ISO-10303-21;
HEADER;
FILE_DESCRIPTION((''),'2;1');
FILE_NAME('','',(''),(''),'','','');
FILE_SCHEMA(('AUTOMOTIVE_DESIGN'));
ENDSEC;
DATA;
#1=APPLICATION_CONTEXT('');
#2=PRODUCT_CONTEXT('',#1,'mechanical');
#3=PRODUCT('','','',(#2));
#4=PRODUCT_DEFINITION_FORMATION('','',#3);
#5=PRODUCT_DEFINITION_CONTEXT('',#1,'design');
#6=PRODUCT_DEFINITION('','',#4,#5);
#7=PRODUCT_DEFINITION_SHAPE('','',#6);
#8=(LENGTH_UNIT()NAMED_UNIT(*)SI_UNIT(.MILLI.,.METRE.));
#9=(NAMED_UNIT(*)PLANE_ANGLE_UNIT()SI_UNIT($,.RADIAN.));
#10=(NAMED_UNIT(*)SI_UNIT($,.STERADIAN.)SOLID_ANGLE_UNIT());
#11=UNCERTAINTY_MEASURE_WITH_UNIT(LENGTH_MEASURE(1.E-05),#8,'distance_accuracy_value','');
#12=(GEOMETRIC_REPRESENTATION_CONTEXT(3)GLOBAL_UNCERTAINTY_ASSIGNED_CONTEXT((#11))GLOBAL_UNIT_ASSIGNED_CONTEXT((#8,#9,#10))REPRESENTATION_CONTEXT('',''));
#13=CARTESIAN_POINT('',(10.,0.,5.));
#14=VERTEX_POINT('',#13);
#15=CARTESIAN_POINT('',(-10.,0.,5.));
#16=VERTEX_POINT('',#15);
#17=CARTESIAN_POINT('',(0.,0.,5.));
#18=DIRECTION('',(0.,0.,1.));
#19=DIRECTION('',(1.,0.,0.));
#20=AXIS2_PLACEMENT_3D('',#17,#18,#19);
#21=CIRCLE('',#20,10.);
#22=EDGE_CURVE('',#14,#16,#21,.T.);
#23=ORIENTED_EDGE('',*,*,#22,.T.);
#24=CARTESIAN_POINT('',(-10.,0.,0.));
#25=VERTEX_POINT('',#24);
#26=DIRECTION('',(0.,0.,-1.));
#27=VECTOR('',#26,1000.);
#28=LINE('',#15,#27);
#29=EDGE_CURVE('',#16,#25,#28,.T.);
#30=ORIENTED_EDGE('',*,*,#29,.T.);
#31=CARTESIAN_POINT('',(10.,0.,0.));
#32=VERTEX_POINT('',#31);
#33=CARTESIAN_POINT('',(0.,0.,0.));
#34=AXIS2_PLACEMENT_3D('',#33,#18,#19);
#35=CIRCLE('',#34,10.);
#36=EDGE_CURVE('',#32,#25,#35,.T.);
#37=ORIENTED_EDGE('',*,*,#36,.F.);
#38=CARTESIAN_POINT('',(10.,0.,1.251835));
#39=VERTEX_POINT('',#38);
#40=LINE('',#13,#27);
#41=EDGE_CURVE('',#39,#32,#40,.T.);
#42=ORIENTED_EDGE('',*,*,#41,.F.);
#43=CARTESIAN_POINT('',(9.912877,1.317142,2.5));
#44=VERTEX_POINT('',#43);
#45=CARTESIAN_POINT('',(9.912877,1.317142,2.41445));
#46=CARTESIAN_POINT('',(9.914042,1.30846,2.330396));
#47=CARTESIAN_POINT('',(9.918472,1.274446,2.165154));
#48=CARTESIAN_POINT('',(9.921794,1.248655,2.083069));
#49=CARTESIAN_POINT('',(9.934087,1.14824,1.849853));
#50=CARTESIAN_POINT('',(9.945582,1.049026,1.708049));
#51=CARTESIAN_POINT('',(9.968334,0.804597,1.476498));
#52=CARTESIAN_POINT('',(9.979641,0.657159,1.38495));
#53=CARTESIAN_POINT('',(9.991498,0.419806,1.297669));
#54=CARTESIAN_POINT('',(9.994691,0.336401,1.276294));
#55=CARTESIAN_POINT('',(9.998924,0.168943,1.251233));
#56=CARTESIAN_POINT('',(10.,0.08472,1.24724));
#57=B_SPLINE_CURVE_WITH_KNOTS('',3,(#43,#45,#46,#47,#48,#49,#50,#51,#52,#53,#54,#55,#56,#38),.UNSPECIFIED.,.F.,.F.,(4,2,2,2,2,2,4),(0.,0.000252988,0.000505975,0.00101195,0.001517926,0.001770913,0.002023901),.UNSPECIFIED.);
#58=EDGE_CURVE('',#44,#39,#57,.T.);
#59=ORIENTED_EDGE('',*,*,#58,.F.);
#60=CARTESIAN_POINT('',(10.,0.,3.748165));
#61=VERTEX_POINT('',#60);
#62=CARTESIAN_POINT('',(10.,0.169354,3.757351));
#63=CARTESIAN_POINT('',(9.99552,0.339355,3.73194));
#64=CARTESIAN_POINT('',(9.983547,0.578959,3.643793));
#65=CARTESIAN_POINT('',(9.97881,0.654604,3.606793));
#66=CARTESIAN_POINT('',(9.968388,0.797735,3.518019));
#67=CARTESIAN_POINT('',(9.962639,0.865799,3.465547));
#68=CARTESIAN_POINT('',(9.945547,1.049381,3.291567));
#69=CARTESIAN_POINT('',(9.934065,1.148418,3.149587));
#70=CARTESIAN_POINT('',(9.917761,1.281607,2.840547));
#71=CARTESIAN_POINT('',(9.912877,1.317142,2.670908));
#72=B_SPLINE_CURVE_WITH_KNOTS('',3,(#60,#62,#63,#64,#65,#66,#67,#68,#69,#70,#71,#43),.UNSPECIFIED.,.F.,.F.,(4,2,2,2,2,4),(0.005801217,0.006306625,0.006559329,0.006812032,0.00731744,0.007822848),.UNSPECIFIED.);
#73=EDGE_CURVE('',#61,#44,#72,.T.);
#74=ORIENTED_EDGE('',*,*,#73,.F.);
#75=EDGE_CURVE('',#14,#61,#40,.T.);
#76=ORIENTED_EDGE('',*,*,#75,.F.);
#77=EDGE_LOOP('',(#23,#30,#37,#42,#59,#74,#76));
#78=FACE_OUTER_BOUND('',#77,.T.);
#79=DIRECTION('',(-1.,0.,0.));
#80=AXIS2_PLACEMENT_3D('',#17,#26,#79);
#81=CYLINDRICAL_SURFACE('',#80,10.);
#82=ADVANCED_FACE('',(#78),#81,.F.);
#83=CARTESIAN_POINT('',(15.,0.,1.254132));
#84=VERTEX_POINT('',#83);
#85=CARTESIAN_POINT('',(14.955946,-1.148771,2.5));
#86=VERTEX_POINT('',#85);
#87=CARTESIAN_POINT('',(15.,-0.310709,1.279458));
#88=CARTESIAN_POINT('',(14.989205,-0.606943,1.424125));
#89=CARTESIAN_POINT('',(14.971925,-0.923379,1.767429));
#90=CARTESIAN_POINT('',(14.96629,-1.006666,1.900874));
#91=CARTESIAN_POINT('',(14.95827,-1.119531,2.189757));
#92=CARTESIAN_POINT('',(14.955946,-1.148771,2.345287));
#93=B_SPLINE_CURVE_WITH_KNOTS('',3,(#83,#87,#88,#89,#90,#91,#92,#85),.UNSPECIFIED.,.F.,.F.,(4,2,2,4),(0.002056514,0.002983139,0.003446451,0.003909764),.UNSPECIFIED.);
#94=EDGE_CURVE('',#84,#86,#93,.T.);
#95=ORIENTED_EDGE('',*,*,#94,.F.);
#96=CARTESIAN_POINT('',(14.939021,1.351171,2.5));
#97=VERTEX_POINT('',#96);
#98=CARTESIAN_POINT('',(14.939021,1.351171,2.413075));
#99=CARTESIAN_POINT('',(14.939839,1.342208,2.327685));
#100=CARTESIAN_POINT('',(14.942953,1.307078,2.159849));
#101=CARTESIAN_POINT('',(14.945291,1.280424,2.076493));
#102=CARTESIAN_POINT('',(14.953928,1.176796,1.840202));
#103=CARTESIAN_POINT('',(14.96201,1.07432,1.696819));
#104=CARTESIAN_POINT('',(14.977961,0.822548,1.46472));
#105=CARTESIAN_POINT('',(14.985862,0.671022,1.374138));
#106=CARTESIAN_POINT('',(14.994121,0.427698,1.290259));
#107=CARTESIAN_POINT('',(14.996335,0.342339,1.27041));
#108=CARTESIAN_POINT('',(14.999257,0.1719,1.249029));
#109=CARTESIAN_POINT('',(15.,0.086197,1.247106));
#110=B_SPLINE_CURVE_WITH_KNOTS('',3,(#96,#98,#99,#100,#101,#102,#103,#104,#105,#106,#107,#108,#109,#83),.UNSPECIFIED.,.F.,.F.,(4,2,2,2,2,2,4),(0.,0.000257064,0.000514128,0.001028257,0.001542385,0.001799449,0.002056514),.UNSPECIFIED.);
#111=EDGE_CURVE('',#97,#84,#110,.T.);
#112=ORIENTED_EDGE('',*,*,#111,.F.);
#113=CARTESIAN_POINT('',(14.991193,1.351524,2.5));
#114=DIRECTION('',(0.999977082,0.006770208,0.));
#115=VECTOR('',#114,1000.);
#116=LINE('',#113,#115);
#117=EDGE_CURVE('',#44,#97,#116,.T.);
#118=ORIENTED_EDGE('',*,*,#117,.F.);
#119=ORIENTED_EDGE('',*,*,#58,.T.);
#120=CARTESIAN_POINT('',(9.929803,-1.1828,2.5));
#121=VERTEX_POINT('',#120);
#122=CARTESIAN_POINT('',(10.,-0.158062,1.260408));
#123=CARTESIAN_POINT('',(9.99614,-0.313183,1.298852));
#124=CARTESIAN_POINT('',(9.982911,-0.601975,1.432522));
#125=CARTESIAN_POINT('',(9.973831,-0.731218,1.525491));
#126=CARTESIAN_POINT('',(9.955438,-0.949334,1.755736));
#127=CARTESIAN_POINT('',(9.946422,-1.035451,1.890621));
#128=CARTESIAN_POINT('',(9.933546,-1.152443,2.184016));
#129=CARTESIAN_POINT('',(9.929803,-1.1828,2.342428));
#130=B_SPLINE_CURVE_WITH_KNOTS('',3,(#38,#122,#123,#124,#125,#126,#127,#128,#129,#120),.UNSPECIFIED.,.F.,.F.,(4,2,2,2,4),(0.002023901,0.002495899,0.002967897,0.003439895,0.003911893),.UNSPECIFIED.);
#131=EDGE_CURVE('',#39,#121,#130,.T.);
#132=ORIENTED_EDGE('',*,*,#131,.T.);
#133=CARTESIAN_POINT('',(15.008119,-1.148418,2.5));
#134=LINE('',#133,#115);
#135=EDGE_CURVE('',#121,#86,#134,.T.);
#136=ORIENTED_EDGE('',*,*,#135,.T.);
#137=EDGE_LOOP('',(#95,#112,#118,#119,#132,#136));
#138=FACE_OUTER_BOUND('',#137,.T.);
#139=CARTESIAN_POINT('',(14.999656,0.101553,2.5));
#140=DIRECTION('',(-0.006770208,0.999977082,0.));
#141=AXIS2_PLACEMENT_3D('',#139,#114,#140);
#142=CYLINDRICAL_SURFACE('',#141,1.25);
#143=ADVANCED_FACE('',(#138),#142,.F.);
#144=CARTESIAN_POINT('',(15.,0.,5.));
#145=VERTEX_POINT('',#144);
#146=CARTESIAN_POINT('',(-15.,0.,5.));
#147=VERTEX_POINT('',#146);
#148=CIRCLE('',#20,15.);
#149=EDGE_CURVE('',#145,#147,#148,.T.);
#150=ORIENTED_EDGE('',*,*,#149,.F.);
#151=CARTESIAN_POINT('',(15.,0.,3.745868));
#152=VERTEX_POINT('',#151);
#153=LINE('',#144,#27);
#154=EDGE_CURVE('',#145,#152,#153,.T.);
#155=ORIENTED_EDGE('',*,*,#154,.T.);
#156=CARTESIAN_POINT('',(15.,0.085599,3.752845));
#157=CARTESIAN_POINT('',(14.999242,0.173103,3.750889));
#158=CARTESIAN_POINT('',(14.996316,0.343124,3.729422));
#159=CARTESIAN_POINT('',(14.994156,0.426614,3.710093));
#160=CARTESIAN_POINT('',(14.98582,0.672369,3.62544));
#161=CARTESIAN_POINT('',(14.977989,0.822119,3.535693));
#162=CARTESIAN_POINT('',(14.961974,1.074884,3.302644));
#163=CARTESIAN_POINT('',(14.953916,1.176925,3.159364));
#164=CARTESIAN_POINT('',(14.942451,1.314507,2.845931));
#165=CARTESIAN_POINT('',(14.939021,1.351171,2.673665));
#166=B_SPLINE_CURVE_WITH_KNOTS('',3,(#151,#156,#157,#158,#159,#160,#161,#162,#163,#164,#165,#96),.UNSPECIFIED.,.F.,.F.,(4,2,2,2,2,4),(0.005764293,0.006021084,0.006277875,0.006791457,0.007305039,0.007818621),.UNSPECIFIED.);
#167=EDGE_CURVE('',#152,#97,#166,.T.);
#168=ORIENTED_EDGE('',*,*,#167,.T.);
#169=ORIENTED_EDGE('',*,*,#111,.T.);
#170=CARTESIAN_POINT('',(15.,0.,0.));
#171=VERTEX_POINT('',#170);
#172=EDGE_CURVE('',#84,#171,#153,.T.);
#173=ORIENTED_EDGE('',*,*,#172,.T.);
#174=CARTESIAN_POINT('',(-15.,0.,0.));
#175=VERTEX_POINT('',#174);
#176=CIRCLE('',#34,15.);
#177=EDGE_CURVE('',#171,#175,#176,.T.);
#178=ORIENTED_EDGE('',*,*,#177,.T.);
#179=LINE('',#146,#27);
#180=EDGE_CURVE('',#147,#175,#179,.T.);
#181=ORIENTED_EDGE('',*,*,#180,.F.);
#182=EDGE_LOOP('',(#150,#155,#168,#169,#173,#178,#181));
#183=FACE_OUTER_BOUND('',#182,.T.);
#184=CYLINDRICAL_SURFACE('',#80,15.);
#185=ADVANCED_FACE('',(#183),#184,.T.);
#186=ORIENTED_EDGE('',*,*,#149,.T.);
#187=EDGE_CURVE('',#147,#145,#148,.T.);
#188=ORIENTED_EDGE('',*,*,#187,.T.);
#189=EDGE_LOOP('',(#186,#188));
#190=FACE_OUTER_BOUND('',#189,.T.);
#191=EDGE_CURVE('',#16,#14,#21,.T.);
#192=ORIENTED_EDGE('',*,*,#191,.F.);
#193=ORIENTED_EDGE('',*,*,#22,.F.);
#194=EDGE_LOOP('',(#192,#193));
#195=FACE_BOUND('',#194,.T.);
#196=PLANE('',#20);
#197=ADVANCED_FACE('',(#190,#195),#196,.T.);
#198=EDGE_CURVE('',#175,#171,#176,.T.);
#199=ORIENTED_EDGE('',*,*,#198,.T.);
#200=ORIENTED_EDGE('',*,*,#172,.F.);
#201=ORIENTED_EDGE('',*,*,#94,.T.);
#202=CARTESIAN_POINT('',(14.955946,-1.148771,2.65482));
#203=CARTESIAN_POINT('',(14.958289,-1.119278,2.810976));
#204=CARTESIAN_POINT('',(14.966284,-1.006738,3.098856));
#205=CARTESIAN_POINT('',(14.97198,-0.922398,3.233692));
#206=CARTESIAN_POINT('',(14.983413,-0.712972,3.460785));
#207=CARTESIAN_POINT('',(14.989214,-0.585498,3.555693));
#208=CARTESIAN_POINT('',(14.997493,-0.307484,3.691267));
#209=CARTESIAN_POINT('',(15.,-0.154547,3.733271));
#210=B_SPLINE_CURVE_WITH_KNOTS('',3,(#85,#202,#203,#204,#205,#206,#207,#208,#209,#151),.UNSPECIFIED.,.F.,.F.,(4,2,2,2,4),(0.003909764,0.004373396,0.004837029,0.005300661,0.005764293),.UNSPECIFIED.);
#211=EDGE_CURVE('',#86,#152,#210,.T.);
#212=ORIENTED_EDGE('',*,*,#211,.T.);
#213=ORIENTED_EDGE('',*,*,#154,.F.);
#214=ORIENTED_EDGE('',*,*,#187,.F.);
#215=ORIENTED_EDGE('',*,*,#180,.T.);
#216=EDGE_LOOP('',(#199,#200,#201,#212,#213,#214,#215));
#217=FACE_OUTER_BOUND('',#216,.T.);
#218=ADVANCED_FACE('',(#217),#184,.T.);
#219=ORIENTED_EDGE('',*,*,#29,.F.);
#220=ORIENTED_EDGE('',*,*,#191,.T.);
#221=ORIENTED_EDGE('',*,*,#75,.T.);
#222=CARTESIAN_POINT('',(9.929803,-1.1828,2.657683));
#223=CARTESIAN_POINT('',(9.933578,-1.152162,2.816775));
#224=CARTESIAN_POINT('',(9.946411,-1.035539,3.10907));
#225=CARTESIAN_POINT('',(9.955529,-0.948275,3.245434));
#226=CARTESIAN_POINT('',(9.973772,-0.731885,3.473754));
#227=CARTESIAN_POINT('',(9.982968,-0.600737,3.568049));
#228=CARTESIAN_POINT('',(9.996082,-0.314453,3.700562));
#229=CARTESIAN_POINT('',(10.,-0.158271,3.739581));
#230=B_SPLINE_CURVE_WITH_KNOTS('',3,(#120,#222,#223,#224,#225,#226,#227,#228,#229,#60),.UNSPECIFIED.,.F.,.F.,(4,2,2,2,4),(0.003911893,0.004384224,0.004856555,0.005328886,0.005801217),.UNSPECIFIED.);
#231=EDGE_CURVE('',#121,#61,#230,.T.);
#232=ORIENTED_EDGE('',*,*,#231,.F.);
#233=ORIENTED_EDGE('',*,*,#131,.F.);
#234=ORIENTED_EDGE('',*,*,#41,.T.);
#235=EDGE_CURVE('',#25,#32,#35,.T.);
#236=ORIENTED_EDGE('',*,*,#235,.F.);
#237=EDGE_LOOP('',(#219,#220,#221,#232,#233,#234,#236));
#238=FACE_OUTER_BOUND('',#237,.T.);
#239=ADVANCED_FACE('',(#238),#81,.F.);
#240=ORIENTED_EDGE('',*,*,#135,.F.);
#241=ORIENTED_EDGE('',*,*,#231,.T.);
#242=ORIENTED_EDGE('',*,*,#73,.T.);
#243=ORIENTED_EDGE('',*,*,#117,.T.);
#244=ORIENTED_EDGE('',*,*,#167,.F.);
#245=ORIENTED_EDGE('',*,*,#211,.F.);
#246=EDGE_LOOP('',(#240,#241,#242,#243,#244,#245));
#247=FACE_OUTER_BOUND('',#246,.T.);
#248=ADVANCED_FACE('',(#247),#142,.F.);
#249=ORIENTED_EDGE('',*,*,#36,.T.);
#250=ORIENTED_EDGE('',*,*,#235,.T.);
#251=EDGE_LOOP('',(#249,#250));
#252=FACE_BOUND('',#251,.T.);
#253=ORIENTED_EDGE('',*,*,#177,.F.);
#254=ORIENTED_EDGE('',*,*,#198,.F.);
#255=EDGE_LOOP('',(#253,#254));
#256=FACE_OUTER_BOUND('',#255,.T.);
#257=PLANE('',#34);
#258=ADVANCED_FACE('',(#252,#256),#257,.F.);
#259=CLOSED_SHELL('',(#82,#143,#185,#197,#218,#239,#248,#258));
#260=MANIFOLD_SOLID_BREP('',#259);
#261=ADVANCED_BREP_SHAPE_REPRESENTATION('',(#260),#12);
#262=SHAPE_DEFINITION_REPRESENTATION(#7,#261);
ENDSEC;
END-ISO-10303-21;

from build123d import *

# Parameters (mm, degrees)
SKETCH_1_R             = 15
SKETCH_1_R_2           = 10
EXTRUDE_1_DEPTH        = 5
HOLE_WIZARD_M3_2_D     = 2.5
HOLE_WIZARD_M3_2_DEPTH = 7.5
HOLE_WIZARD_M3_2_TIP   = 0.751075774


with BuildPart() as part:
    # 草图1 → 凸台-拉伸1 (new body)
    with BuildSketch(Plane.XY):
        Circle(SKETCH_1_R)
        Circle(SKETCH_1_R_2, mode=Mode.SUBTRACT)
    extrude(amount=EXTRUDE_1_DEPTH)

    # M3 螺纹孔2
    with Locations(Plane(origin=(14.999656228, 0.101553124, 2.5), x_dir=(-0.006770208298, 0.999977081877, 0), z_dir=(0.999977081877, 0.006770208298, 0))):
        with Locations((0, 0)):
            Hole(HOLE_WIZARD_M3_2_D / 2, depth=HOLE_WIZARD_M3_2_DEPTH)
            with Locations((0, 0, -(HOLE_WIZARD_M3_2_DEPTH + HOLE_WIZARD_M3_2_TIP / 2))):  # 118° drill point
                Cone(0, HOLE_WIZARD_M3_2_D / 2, HOLE_WIZARD_M3_2_TIP, mode=Mode.SUBTRACT)


solid = part.part
